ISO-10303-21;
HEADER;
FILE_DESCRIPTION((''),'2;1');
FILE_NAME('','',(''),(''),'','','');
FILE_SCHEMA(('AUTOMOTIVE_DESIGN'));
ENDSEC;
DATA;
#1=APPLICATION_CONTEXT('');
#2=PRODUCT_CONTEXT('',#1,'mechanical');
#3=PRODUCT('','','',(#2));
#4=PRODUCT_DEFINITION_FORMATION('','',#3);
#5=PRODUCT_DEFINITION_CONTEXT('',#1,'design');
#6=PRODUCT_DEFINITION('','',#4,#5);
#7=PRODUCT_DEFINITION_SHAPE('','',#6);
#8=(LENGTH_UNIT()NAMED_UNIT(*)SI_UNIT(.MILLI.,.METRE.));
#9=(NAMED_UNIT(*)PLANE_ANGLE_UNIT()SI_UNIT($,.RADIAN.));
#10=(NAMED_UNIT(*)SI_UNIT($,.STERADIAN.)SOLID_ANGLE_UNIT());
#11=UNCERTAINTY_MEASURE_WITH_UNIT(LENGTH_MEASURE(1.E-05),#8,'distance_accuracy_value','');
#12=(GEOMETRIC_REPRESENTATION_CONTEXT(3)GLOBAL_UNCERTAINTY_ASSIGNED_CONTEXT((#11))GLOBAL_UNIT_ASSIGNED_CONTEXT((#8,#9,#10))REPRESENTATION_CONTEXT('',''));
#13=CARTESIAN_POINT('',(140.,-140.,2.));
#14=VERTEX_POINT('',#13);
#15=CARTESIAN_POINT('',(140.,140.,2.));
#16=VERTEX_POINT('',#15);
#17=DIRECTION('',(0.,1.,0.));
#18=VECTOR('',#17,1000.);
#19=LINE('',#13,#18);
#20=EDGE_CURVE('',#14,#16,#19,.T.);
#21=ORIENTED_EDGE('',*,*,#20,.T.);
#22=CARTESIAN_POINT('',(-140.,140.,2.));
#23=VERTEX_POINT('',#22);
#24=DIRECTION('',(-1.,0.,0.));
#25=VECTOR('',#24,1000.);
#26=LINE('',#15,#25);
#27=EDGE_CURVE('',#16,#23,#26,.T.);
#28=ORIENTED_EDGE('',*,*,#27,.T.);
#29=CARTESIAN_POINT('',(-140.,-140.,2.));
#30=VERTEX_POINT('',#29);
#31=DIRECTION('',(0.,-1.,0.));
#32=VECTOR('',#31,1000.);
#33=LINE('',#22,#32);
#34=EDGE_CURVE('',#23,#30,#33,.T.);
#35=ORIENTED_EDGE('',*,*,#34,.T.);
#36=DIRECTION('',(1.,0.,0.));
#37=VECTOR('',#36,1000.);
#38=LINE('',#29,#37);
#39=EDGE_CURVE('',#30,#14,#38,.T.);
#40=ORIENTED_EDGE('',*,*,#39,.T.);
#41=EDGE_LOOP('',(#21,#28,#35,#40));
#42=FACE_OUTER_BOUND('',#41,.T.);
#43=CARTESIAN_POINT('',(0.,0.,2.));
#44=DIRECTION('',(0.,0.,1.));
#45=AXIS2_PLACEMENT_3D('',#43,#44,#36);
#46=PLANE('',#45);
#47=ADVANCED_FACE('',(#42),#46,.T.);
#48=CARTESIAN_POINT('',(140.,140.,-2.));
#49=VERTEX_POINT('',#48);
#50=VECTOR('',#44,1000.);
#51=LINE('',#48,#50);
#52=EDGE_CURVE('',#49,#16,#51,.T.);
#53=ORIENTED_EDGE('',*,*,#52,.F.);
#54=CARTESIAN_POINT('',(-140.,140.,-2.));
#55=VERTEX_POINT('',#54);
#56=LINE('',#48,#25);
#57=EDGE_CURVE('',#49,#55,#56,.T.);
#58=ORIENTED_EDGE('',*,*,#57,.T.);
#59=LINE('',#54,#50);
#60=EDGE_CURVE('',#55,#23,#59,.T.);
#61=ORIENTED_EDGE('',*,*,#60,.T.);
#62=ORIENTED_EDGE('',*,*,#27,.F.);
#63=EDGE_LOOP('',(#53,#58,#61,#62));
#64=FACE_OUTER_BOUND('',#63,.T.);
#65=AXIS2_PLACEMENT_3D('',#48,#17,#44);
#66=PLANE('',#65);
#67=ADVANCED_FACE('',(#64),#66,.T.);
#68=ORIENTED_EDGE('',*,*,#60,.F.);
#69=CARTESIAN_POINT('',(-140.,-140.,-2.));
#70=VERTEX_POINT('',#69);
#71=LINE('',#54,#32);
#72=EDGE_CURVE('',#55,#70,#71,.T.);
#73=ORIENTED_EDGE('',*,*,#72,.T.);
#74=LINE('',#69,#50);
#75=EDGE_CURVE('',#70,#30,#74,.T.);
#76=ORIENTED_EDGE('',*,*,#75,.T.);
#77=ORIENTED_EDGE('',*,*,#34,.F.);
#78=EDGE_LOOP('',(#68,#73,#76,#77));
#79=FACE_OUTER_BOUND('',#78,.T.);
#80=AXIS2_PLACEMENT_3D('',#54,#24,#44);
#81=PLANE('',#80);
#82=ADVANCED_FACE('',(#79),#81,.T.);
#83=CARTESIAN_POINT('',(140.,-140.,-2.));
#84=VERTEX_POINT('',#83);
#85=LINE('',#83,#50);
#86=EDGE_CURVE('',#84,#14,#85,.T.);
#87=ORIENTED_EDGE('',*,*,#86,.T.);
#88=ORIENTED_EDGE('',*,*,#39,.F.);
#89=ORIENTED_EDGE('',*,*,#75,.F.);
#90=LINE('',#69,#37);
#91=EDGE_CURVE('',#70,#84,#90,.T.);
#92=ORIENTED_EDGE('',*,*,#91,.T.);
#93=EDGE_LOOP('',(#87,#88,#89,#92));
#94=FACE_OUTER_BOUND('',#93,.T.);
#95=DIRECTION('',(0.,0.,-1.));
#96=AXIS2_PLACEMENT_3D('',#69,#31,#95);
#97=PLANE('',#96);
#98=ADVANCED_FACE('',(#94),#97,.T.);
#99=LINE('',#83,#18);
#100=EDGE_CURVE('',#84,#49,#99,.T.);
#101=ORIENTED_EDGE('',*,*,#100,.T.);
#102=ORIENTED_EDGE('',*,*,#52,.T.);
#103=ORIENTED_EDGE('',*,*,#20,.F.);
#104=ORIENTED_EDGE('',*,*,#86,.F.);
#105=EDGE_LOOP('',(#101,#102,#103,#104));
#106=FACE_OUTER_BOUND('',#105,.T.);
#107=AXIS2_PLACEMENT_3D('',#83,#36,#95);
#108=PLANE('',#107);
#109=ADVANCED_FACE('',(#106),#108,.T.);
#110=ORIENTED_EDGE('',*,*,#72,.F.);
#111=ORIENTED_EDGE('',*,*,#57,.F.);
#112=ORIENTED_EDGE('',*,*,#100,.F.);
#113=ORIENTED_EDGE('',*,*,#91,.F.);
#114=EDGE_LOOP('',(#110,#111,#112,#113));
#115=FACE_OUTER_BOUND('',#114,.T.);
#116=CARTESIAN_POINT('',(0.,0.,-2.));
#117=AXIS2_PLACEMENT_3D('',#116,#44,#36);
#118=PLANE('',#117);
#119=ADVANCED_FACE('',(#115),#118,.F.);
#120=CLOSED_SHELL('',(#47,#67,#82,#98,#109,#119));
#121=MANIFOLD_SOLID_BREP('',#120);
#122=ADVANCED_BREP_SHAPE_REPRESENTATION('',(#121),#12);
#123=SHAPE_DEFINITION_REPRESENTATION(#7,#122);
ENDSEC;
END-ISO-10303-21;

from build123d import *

# Parameters (mm, degrees)
SKETCH_1_W      = 280
SKETCH_1_H      = 280
EXTRUDE_1_DEPTH = 2


with BuildPart() as part:
    # 草图1 → 凸台-拉伸1 (new, symmetric)
    with BuildSketch(Plane.XY):
        Rectangle(SKETCH_1_W, SKETCH_1_H)
    extrude(amount=EXTRUDE_1_DEPTH, both=True)


solid = part.part
